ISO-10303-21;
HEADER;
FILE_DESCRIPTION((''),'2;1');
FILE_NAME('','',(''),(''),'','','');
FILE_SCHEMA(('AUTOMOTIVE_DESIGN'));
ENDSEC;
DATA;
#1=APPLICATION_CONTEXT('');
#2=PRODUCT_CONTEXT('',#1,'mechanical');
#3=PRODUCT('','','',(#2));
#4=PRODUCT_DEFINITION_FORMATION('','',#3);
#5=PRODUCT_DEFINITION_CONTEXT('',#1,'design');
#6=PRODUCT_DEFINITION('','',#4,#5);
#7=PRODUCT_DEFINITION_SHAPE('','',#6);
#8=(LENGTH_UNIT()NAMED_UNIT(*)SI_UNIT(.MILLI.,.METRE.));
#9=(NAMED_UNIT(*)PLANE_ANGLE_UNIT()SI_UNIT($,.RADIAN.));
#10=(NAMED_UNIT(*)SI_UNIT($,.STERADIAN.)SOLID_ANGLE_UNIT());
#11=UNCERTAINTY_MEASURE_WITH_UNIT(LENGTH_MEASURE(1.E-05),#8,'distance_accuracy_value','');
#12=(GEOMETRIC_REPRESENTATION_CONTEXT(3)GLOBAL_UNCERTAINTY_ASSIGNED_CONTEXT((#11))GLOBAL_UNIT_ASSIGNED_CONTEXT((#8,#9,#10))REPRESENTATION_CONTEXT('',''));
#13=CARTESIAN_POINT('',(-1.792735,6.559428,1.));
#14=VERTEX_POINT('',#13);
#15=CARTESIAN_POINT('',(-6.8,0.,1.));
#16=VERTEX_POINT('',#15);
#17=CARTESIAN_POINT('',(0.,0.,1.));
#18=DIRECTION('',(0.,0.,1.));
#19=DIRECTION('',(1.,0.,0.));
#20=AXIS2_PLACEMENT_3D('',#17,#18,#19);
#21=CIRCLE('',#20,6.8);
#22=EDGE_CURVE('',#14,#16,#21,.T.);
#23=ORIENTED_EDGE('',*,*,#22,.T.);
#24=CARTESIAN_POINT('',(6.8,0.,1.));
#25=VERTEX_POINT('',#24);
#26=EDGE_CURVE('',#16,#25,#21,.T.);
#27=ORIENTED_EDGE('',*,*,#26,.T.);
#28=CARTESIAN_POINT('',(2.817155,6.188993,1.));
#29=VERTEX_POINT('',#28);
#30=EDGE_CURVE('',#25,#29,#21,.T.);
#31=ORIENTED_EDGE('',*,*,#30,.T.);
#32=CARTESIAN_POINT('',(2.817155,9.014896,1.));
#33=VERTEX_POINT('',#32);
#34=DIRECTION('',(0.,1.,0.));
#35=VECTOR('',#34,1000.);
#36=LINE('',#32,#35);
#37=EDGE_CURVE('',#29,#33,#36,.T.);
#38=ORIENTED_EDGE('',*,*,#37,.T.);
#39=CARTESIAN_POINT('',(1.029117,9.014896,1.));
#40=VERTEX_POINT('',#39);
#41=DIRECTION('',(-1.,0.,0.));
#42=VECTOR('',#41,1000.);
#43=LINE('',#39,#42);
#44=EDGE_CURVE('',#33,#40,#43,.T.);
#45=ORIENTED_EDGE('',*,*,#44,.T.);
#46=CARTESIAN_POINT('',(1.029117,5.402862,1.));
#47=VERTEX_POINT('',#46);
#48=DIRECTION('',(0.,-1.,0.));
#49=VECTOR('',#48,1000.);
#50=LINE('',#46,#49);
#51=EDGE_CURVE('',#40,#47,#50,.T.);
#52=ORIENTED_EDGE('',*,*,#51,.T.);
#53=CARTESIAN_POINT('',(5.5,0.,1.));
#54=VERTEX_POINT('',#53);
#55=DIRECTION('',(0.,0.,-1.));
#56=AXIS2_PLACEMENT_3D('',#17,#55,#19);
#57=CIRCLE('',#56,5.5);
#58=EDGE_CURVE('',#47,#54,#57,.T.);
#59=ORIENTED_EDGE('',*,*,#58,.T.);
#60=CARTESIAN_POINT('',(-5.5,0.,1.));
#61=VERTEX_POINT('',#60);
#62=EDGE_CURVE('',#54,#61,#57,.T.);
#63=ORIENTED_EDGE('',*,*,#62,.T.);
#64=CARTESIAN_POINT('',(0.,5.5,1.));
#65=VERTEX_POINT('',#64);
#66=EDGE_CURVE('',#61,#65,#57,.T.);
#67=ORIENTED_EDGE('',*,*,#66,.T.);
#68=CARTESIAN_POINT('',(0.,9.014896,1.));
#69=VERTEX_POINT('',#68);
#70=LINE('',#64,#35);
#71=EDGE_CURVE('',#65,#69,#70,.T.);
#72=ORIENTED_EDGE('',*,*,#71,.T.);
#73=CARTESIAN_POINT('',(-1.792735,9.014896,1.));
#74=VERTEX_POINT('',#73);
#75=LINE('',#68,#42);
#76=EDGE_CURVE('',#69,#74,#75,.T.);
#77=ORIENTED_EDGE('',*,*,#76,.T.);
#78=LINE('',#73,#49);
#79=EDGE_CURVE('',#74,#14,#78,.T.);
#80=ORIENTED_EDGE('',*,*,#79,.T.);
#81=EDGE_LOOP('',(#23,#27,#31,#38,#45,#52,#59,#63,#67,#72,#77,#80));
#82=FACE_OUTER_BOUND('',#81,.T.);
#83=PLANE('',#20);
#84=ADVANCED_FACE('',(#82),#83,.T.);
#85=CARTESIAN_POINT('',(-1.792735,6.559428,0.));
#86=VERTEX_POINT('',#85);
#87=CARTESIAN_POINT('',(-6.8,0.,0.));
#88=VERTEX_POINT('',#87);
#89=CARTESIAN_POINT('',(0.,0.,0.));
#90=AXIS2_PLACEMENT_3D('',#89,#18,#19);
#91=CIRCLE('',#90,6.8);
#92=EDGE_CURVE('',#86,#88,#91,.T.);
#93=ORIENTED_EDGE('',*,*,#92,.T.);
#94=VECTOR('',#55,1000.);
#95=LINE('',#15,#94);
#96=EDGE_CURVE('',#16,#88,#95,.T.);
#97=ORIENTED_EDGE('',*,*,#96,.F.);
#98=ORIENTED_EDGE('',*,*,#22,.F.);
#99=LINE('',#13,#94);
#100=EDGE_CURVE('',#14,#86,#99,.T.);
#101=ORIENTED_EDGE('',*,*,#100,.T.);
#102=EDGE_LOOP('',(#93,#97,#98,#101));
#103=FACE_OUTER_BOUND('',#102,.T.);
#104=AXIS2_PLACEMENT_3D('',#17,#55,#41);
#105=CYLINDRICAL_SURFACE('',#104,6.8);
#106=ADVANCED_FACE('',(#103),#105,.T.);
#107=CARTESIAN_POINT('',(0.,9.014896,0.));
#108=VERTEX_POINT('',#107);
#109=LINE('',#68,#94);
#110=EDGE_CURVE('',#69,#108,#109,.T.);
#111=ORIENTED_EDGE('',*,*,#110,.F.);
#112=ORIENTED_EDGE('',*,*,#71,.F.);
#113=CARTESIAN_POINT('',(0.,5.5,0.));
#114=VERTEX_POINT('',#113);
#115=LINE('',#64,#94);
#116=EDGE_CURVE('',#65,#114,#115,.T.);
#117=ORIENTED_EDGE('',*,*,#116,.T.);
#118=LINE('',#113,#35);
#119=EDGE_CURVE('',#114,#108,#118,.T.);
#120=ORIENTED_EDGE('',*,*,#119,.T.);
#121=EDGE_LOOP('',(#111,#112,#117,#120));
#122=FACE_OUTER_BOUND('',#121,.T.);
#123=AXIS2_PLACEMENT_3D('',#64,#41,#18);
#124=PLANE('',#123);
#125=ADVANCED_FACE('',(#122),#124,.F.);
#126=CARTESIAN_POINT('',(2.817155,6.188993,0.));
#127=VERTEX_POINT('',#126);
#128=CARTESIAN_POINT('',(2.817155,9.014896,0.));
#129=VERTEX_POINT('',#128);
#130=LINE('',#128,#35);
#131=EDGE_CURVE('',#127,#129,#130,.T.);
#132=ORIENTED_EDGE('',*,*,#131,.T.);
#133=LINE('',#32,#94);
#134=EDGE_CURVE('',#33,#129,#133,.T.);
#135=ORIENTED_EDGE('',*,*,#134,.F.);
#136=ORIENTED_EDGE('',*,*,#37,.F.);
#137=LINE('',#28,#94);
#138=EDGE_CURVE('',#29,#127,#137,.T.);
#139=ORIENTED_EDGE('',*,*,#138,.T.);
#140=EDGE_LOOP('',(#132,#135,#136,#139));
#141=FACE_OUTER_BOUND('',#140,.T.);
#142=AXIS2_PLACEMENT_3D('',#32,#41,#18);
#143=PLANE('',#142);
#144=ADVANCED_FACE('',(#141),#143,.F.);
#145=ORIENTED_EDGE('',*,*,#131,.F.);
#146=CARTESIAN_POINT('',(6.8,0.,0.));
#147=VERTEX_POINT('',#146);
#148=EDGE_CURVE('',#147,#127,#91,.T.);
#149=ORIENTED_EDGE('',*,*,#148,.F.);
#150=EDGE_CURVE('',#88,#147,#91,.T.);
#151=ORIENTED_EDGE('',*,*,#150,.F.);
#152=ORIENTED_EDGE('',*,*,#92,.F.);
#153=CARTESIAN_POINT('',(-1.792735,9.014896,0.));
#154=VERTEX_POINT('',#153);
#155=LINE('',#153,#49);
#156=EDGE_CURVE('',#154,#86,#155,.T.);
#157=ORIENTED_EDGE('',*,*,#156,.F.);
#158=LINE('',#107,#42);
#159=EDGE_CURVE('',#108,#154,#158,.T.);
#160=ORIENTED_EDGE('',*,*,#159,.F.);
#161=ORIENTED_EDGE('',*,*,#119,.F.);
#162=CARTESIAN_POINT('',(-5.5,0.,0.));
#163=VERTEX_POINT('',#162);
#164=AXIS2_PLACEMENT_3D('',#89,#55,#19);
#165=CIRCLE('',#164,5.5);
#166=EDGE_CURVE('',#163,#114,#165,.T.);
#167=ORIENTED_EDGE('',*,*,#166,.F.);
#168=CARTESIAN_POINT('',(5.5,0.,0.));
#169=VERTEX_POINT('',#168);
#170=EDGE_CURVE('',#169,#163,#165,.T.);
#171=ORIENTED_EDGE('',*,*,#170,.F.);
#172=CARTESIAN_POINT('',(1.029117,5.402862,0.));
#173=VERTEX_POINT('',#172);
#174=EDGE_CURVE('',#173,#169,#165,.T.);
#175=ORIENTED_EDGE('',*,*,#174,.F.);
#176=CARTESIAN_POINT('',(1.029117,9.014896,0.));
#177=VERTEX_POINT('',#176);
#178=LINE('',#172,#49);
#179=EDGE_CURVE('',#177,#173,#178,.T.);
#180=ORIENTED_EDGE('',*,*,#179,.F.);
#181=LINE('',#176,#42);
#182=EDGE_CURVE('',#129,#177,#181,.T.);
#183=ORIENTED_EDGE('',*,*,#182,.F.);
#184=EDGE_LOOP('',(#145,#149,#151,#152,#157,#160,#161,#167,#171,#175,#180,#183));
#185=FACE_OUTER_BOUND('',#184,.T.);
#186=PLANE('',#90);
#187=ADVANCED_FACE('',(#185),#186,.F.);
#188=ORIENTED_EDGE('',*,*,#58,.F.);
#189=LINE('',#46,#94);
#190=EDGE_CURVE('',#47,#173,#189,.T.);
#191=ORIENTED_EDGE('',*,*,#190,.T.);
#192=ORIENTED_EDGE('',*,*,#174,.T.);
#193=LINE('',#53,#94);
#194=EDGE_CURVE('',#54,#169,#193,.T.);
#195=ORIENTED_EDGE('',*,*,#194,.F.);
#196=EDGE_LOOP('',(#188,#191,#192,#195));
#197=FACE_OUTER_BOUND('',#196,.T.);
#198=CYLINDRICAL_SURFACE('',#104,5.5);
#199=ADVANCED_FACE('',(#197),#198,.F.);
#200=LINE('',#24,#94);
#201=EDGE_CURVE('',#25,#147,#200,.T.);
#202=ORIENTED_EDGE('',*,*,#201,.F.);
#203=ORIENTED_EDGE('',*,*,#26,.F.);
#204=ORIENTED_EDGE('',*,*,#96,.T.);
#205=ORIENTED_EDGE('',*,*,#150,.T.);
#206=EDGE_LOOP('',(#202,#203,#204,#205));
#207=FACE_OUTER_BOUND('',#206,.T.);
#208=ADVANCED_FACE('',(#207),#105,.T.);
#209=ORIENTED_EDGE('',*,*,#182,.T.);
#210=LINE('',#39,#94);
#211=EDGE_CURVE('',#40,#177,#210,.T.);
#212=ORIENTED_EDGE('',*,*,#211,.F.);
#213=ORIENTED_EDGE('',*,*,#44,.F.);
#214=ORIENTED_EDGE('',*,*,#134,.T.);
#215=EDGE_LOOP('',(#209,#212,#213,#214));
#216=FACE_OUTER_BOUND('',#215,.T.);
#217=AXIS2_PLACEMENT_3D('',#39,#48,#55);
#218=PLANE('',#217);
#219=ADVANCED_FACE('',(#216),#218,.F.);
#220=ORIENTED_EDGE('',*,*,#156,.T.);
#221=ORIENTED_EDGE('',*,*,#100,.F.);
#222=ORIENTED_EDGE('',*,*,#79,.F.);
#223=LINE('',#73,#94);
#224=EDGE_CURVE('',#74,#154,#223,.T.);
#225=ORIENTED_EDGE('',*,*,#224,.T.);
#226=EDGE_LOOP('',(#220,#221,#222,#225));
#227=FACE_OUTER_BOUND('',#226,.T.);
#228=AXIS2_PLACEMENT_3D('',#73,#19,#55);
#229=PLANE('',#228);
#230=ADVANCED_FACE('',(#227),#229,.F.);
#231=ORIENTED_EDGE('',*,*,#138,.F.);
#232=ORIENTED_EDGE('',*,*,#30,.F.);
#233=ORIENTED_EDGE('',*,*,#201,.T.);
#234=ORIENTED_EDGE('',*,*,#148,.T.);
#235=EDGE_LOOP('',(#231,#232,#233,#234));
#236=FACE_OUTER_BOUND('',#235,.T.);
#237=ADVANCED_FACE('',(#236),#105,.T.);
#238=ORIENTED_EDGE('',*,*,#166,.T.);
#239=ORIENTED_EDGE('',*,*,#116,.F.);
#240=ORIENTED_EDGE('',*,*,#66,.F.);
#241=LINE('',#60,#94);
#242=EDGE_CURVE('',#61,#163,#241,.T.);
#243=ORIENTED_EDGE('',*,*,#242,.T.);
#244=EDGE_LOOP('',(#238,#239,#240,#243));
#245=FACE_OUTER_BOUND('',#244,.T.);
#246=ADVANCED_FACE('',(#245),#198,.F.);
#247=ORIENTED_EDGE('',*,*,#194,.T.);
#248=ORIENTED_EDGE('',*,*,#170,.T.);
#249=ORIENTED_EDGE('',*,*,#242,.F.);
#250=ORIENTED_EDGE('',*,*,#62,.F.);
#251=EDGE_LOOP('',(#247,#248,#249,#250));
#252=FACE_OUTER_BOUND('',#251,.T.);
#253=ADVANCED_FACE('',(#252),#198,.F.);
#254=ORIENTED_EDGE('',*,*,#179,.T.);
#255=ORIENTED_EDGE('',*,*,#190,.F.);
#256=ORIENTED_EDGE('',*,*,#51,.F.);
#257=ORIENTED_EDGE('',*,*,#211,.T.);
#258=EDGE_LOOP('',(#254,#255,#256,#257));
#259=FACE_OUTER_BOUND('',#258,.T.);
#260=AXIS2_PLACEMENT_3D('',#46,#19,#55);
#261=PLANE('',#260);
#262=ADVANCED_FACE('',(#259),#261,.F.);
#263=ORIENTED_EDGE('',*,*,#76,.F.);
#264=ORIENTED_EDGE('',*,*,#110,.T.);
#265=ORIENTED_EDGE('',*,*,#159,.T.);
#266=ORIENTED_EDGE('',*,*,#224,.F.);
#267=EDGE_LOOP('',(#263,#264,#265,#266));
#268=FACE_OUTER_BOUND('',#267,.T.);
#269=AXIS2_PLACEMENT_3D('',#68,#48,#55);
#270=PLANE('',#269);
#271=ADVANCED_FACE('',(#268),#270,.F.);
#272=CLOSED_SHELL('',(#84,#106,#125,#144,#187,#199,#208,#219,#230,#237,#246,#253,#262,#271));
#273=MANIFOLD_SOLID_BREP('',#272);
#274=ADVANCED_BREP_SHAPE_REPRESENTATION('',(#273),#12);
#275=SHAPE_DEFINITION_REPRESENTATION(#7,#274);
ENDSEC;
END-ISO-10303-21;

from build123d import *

# Parameters (mm, degrees)
BOSS_EXTRUDE1_DEPTH = 1


with BuildPart() as part:
    # Sketch1 → Boss-Extrude1 (new body)
    with BuildSketch(Plane.XY):
        with BuildLine():
            Line((1.029116593, 5.402862115), (1.029116593, 9.014895643))
            Line((1.029116593, 9.014895643), (2.817154888, 9.014895643))
            Line((2.817154888, 9.014895643), (2.817154888, 6.188993322))
            ThreePointArc((2.817154888, 6.188993322), (-0.544669265, -6.778151326), (-1.792734929, 6.559428441))
            Line((-1.792734929, 6.559428441), (-1.792734929, 9.014895643))
            Line((-1.792734929, 9.014895643), (0, 9.014895643))
            Line((0, 9.014895643), (0, 5.5))
            ThreePointArc((0, 5.5), (-0.516845415, -5.475661678), (1.029116593, 5.402862115))
        make_face()
    extrude(amount=BOSS_EXTRUDE1_DEPTH)


solid = part.part
